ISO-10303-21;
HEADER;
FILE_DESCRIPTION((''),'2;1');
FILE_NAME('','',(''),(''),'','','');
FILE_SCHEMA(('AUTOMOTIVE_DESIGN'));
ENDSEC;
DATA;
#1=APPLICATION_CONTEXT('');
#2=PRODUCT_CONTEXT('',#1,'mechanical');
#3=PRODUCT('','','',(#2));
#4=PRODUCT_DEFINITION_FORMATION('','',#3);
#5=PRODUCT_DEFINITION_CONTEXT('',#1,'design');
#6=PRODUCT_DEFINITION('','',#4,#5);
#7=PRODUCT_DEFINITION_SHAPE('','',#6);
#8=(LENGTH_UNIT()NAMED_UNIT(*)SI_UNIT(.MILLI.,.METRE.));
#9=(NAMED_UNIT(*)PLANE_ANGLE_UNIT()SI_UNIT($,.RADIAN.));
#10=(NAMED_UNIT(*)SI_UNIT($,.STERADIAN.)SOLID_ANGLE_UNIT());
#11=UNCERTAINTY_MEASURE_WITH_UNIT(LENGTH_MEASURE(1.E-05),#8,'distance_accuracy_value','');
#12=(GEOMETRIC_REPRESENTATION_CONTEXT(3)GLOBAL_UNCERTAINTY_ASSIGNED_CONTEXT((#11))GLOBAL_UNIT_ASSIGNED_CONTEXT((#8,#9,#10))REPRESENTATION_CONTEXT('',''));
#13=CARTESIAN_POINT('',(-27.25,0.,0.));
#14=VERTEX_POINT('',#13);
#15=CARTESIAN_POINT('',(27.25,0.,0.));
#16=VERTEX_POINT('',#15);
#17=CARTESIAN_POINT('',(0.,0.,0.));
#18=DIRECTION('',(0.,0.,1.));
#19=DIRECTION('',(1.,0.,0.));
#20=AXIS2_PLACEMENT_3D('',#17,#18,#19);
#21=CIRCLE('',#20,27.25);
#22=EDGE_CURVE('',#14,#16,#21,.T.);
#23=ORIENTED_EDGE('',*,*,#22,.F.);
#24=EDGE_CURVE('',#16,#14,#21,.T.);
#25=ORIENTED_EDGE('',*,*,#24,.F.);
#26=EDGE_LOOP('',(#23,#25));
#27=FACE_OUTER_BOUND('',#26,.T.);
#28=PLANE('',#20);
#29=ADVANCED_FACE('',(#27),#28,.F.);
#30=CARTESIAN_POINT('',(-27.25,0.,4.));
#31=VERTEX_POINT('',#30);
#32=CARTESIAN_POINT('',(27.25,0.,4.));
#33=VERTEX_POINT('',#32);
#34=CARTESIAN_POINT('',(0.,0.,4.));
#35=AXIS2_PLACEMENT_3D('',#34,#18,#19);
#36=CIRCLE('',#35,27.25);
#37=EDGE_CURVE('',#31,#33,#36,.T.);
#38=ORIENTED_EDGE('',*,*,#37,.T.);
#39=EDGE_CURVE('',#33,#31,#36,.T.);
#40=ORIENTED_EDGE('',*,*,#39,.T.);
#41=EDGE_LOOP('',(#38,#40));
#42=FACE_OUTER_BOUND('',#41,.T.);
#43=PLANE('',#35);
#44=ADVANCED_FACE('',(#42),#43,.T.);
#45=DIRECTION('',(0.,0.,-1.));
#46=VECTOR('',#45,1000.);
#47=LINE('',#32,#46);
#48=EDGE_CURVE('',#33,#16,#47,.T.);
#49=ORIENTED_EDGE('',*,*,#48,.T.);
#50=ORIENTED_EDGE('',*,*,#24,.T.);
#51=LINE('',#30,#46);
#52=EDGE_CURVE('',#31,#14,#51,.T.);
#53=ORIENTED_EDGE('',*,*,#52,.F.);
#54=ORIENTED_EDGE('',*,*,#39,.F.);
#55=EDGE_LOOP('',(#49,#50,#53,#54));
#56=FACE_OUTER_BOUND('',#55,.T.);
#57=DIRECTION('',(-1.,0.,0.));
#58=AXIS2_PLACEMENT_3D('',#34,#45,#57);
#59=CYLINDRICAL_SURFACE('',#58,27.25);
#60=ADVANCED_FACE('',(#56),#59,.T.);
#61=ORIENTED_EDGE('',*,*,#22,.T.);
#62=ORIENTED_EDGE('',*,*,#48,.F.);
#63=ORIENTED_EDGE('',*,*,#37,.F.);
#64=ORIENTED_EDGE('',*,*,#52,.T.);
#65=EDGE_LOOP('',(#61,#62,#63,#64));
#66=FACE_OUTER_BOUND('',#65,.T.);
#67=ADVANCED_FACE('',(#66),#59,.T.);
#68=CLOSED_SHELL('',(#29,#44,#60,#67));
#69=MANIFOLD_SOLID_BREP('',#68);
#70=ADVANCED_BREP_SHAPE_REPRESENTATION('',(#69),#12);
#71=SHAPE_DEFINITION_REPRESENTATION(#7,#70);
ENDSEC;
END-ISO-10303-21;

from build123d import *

# Parameters (mm, degrees)
SKETCH_1_R      = 27.25
EXTRUDE_1_DEPTH = 4


with BuildPart() as part:
    # 草图1 → 凸台-拉伸1 (new body)
    with BuildSketch(Plane.XY):
        Circle(SKETCH_1_R)
    extrude(amount=EXTRUDE_1_DEPTH)


solid = part.part
